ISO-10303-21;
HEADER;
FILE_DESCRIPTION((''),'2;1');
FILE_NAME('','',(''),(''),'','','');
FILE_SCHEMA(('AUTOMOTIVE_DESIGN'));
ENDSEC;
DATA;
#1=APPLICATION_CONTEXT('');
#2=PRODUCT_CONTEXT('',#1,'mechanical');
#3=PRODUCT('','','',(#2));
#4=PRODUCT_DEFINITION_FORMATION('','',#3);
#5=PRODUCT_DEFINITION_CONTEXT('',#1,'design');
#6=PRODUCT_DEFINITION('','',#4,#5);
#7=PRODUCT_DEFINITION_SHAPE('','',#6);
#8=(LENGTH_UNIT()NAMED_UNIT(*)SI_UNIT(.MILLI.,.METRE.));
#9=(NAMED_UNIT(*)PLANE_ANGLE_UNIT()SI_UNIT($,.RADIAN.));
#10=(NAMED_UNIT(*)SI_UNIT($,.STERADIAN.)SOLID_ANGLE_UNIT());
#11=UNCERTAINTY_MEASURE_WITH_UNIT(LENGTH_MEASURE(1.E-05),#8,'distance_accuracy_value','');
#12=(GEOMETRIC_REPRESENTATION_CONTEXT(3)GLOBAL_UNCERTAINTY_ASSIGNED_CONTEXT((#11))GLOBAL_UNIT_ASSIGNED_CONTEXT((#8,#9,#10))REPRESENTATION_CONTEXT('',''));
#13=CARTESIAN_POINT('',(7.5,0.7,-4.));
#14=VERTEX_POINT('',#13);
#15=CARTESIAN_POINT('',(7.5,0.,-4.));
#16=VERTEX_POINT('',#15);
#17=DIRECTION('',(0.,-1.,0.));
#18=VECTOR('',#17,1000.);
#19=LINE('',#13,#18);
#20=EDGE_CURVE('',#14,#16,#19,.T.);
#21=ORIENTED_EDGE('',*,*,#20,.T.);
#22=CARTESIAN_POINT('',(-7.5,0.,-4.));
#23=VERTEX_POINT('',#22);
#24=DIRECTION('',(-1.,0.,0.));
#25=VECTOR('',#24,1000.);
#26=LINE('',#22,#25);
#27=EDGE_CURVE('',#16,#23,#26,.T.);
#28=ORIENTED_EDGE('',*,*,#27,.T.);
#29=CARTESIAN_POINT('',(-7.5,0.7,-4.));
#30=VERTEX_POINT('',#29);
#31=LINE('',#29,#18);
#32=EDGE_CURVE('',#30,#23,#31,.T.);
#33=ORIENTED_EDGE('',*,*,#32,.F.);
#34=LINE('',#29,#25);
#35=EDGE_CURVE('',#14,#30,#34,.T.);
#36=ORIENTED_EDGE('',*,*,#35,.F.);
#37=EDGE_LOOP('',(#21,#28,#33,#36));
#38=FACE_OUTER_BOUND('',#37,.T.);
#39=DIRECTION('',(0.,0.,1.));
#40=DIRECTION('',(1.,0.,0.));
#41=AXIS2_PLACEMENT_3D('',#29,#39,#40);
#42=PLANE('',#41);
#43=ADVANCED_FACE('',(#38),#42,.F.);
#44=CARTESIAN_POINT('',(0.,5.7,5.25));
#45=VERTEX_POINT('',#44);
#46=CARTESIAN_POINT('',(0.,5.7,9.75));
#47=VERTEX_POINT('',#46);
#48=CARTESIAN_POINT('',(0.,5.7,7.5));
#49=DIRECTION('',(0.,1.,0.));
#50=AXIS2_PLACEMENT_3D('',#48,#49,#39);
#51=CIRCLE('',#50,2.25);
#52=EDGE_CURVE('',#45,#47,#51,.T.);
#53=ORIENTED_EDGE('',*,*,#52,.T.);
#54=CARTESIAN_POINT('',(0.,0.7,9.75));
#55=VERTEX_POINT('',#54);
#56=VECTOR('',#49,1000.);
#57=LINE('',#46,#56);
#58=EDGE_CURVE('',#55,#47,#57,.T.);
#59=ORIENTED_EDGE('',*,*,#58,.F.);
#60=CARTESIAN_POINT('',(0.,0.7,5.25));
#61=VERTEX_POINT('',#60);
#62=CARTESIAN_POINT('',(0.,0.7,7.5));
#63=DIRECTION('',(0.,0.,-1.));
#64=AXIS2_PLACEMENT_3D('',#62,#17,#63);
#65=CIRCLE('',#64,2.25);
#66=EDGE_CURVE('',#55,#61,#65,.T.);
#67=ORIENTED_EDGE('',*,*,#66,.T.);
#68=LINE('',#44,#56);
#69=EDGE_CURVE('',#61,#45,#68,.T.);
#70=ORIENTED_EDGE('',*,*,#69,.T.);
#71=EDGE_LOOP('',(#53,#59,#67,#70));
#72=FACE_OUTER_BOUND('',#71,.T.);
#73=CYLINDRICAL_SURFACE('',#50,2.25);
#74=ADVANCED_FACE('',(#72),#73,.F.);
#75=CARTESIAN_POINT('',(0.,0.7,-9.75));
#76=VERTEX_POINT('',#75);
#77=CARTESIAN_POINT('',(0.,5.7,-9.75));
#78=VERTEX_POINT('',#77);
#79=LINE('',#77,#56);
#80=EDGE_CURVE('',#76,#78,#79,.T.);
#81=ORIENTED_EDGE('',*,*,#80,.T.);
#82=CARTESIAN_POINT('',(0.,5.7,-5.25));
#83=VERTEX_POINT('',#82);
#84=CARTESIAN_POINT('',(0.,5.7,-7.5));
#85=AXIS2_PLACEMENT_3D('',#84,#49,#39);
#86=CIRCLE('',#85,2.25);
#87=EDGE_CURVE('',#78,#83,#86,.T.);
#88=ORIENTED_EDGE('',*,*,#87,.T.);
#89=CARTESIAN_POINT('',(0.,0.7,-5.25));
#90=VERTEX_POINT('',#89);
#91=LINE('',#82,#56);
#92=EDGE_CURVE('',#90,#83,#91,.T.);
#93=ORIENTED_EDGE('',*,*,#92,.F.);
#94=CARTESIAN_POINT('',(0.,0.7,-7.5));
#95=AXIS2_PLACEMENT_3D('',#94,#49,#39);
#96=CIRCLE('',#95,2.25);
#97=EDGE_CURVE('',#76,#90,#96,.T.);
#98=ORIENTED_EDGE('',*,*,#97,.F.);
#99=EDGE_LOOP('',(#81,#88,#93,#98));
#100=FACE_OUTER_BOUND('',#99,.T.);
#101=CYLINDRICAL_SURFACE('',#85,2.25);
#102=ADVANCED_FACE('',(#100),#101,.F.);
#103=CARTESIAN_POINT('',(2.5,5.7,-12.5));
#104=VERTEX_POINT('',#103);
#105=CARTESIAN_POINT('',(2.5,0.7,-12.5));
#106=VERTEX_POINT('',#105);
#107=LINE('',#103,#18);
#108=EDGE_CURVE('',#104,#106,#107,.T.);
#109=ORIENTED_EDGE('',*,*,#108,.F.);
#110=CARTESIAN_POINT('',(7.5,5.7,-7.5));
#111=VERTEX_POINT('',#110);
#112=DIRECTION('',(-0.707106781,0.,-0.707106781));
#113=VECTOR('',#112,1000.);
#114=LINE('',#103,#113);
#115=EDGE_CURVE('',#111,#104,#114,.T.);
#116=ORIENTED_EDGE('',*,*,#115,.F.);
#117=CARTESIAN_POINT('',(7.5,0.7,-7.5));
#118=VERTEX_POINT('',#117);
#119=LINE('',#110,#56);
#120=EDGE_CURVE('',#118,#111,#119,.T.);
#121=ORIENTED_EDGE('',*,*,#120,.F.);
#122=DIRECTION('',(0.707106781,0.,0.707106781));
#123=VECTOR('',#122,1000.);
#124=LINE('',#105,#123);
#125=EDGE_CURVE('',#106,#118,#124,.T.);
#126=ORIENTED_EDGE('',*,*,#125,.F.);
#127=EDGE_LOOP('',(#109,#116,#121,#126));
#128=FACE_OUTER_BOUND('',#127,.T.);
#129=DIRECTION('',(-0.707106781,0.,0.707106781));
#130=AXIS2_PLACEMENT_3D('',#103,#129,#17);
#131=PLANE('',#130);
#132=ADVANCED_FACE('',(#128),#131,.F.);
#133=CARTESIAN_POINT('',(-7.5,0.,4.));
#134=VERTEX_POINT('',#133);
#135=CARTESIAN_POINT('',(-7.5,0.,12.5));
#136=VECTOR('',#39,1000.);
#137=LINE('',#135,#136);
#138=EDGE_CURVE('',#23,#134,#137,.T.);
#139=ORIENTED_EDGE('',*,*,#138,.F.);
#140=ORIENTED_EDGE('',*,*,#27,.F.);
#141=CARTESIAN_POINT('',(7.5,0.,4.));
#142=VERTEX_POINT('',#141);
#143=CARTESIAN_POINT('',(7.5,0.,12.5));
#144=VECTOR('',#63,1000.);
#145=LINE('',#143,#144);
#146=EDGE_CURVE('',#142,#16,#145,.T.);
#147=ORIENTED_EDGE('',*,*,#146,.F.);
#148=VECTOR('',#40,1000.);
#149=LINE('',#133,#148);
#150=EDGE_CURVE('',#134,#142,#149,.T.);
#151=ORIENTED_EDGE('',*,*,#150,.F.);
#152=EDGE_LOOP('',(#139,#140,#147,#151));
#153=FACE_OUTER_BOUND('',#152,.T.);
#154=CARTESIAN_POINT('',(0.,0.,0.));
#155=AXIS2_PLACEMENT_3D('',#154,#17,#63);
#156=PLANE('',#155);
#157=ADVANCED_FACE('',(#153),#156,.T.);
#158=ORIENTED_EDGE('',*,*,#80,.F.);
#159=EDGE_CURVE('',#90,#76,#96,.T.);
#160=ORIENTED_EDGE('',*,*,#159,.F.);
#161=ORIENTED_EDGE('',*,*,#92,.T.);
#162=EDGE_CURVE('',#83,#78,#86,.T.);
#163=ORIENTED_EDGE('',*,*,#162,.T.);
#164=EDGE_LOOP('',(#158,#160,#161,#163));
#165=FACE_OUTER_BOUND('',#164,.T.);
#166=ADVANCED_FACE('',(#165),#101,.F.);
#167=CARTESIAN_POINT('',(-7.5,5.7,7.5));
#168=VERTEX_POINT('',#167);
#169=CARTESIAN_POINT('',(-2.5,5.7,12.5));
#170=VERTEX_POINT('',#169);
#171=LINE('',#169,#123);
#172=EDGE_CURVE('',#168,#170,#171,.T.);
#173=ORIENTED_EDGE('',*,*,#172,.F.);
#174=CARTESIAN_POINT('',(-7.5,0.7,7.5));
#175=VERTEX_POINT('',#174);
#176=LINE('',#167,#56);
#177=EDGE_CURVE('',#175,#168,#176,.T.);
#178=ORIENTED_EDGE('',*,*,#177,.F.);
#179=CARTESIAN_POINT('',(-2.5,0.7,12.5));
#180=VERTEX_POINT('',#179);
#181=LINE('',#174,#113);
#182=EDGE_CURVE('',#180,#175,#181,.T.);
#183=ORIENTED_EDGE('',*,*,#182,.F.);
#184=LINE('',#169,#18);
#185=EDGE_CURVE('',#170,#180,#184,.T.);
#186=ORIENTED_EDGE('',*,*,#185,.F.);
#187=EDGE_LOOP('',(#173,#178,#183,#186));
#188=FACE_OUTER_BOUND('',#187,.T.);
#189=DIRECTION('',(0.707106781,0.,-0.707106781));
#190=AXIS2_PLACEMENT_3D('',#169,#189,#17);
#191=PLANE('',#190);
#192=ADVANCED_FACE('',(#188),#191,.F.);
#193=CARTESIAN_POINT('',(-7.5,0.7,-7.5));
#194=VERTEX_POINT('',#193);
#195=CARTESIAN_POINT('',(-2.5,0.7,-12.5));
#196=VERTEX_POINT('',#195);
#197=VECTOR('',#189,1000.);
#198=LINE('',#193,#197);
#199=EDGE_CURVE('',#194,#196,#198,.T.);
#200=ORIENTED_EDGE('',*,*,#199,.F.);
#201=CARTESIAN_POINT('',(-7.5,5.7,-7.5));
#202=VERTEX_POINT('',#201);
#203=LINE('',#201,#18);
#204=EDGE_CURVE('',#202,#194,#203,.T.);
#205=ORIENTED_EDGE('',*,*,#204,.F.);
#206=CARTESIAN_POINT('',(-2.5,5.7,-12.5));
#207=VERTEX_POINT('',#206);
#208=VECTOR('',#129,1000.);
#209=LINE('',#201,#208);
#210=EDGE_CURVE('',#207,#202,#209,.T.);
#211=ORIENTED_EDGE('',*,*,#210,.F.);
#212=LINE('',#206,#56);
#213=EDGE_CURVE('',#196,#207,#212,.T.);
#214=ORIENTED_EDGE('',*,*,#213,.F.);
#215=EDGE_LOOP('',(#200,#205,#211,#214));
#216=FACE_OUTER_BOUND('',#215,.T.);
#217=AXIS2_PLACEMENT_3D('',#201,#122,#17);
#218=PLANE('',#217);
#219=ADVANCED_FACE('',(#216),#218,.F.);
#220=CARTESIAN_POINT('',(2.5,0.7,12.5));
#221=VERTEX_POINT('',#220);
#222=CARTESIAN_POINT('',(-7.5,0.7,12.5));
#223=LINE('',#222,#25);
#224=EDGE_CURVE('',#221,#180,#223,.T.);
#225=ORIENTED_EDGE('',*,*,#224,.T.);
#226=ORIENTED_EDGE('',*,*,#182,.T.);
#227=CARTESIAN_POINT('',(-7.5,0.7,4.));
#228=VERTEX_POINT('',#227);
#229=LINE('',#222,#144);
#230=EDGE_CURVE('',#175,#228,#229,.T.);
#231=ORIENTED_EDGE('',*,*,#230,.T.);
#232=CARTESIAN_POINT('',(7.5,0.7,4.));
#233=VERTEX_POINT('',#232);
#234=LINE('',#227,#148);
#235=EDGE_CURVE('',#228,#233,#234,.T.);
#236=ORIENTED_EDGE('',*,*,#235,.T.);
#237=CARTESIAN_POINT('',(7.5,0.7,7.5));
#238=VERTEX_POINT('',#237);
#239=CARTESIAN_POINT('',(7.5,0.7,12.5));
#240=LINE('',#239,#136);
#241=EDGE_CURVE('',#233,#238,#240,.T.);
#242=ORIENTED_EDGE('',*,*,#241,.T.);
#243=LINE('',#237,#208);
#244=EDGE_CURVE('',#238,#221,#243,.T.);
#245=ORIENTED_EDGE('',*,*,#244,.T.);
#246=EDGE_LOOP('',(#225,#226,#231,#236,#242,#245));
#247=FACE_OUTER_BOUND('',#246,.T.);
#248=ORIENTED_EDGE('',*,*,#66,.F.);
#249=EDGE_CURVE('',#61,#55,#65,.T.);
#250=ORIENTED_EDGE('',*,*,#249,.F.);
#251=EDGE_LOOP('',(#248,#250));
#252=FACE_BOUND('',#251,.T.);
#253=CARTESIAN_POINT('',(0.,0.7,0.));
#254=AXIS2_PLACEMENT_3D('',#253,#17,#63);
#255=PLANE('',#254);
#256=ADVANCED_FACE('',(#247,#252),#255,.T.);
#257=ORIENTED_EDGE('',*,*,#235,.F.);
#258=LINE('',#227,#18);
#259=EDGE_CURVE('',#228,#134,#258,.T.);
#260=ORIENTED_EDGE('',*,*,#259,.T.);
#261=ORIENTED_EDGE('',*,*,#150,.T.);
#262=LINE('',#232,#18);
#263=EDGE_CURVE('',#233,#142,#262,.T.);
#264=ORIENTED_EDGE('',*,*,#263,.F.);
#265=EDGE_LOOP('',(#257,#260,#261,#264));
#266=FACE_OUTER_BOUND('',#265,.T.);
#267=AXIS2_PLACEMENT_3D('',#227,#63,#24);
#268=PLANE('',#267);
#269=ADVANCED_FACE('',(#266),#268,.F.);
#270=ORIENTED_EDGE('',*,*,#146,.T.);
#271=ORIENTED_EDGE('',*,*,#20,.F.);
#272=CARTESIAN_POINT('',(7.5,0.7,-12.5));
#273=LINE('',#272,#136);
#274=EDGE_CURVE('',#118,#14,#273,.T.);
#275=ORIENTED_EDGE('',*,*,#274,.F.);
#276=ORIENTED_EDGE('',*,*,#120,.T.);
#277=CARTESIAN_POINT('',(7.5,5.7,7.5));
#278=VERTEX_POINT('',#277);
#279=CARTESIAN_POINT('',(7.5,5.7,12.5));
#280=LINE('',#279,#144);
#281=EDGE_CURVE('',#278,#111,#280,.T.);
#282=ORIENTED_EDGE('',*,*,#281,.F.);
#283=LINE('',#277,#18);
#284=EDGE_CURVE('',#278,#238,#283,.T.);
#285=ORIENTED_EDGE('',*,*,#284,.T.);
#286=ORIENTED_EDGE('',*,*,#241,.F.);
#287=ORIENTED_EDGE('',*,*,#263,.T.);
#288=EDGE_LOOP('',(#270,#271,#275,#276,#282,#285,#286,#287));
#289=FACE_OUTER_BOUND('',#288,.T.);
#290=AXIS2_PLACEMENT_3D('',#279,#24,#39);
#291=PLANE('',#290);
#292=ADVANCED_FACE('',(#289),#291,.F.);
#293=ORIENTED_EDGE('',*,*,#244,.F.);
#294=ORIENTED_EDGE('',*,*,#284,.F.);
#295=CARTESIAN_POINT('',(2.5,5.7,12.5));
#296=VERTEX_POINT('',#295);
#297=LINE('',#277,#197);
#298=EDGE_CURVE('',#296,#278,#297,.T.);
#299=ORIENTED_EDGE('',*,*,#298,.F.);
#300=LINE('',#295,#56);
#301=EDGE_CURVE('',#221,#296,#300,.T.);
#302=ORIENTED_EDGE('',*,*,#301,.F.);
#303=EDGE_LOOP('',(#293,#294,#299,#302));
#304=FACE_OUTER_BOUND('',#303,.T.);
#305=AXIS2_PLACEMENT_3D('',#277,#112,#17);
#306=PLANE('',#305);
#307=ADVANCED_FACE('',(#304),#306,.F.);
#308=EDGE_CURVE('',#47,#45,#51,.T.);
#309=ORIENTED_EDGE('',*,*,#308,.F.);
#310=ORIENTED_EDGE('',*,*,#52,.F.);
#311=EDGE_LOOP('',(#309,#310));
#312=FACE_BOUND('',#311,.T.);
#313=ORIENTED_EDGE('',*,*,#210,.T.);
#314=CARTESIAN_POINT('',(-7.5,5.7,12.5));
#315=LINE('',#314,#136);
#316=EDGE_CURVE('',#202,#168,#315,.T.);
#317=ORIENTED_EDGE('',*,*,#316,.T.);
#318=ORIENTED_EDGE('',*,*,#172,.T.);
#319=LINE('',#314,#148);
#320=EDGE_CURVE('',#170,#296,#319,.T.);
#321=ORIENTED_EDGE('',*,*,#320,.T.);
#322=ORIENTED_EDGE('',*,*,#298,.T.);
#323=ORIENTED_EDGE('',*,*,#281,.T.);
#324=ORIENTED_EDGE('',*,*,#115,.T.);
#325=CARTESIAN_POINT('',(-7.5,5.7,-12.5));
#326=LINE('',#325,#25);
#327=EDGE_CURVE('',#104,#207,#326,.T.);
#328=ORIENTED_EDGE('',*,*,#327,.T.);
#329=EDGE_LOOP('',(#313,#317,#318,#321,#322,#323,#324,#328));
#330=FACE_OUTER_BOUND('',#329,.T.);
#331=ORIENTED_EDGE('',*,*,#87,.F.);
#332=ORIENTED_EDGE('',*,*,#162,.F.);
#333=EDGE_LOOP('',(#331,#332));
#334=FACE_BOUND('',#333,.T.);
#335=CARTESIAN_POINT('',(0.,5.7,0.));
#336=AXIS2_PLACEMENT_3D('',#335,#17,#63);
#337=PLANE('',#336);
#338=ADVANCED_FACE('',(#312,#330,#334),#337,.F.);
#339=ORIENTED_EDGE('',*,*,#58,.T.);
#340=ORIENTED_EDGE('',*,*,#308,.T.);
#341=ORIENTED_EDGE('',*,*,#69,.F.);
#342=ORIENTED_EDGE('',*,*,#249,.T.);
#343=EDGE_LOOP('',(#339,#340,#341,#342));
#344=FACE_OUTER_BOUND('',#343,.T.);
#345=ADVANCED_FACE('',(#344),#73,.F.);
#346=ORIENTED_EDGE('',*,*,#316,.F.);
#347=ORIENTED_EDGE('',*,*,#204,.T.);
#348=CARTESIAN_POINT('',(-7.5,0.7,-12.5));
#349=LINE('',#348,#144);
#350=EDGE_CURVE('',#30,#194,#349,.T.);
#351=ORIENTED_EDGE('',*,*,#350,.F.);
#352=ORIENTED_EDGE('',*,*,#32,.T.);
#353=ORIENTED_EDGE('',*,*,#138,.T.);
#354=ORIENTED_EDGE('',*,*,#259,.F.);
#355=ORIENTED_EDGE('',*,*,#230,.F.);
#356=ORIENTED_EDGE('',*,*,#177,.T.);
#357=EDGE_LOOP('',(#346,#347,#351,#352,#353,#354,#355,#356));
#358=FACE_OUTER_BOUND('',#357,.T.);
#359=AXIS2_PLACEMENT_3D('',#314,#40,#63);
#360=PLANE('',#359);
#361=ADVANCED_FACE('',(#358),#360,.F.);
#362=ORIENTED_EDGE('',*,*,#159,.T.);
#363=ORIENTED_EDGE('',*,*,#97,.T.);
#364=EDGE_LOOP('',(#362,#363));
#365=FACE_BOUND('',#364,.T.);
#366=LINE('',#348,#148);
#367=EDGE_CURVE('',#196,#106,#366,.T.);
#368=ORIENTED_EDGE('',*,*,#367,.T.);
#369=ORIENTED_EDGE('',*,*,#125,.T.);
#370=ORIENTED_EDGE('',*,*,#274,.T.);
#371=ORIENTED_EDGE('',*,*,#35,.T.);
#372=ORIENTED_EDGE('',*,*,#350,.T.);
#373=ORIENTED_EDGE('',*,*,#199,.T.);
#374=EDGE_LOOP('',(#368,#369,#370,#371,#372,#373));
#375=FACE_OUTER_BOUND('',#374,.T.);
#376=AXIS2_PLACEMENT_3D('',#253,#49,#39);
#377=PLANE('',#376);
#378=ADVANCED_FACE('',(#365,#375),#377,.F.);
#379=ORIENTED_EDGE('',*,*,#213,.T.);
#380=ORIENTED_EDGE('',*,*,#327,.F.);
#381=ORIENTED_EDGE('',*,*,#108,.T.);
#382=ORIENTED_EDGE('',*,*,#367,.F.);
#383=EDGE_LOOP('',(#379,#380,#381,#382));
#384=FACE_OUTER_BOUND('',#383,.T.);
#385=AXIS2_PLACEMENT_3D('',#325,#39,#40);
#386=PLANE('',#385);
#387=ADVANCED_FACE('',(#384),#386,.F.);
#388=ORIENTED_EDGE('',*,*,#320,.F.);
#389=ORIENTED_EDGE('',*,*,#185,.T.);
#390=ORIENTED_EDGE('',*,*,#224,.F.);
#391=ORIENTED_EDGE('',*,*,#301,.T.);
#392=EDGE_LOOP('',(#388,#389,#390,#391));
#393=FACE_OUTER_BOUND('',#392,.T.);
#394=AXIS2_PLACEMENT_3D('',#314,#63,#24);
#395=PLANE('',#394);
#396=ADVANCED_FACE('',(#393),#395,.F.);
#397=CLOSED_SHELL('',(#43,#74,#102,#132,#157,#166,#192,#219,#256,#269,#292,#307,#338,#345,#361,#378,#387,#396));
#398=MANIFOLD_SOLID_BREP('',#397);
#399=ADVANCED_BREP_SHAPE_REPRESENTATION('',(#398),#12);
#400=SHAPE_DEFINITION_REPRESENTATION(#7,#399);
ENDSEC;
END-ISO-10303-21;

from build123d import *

# Parameters (mm, degrees)
SKETCH1_W                  = 15
SKETCH1_H                  = 25
BOSS_EXTRUDE1_DEPTH        = 5.7
SKETCH2_W                  = 15
SKETCH2_H                  = 8.5
CUT_EXTRUDE1_DEPTH         = 0.7
CHAMFER1_SIZE              = 5
F_4_5_4_5_DIAMETER_HOLE1_D = 4.5


with BuildPart() as part:
    # Sketch1 → Boss-Extrude1 (new body)
    with BuildSketch(Plane(origin=(0, 0, 0), x_dir=(1, 0, 0), z_dir=(0, 1, 0))):
        Rectangle(SKETCH1_W, SKETCH1_H)
    extrude(amount=BOSS_EXTRUDE1_DEPTH)

    # Sketch2 → Cut-Extrude1 (cut)
    with BuildSketch(Plane.XZ):
        with Locations((0, -8.25)):
            Rectangle(SKETCH2_W, SKETCH2_H)
        with Locations((0, 8.25)):
            Rectangle(SKETCH2_W, SKETCH2_H)
    extrude(amount=-CUT_EXTRUDE1_DEPTH, mode=Mode.SUBTRACT)

    # Chamfer1
    chamfer1_edges = [part.edges().sort_by_distance(p)[0] for p in [
        (7.5, 3.2, 12.5),
        (-7.5, 3.2, 12.5),
        (-7.5, 3.2, -12.5),
        (7.5, 3.2, -12.5),
    ]]
    chamfer(chamfer1_edges, length=CHAMFER1_SIZE)

    # Ø4.5 (4.5) Diameter Hole1 (through all)
    with Locations(Plane(origin=(0, 5.7, 0), x_dir=(1, 0, 0), z_dir=(0, 1, 0))):
        with Locations((0, 7.5), (0, -7.5)):
            Hole(F_4_5_4_5_DIAMETER_HOLE1_D / 2)


solid = part.part
